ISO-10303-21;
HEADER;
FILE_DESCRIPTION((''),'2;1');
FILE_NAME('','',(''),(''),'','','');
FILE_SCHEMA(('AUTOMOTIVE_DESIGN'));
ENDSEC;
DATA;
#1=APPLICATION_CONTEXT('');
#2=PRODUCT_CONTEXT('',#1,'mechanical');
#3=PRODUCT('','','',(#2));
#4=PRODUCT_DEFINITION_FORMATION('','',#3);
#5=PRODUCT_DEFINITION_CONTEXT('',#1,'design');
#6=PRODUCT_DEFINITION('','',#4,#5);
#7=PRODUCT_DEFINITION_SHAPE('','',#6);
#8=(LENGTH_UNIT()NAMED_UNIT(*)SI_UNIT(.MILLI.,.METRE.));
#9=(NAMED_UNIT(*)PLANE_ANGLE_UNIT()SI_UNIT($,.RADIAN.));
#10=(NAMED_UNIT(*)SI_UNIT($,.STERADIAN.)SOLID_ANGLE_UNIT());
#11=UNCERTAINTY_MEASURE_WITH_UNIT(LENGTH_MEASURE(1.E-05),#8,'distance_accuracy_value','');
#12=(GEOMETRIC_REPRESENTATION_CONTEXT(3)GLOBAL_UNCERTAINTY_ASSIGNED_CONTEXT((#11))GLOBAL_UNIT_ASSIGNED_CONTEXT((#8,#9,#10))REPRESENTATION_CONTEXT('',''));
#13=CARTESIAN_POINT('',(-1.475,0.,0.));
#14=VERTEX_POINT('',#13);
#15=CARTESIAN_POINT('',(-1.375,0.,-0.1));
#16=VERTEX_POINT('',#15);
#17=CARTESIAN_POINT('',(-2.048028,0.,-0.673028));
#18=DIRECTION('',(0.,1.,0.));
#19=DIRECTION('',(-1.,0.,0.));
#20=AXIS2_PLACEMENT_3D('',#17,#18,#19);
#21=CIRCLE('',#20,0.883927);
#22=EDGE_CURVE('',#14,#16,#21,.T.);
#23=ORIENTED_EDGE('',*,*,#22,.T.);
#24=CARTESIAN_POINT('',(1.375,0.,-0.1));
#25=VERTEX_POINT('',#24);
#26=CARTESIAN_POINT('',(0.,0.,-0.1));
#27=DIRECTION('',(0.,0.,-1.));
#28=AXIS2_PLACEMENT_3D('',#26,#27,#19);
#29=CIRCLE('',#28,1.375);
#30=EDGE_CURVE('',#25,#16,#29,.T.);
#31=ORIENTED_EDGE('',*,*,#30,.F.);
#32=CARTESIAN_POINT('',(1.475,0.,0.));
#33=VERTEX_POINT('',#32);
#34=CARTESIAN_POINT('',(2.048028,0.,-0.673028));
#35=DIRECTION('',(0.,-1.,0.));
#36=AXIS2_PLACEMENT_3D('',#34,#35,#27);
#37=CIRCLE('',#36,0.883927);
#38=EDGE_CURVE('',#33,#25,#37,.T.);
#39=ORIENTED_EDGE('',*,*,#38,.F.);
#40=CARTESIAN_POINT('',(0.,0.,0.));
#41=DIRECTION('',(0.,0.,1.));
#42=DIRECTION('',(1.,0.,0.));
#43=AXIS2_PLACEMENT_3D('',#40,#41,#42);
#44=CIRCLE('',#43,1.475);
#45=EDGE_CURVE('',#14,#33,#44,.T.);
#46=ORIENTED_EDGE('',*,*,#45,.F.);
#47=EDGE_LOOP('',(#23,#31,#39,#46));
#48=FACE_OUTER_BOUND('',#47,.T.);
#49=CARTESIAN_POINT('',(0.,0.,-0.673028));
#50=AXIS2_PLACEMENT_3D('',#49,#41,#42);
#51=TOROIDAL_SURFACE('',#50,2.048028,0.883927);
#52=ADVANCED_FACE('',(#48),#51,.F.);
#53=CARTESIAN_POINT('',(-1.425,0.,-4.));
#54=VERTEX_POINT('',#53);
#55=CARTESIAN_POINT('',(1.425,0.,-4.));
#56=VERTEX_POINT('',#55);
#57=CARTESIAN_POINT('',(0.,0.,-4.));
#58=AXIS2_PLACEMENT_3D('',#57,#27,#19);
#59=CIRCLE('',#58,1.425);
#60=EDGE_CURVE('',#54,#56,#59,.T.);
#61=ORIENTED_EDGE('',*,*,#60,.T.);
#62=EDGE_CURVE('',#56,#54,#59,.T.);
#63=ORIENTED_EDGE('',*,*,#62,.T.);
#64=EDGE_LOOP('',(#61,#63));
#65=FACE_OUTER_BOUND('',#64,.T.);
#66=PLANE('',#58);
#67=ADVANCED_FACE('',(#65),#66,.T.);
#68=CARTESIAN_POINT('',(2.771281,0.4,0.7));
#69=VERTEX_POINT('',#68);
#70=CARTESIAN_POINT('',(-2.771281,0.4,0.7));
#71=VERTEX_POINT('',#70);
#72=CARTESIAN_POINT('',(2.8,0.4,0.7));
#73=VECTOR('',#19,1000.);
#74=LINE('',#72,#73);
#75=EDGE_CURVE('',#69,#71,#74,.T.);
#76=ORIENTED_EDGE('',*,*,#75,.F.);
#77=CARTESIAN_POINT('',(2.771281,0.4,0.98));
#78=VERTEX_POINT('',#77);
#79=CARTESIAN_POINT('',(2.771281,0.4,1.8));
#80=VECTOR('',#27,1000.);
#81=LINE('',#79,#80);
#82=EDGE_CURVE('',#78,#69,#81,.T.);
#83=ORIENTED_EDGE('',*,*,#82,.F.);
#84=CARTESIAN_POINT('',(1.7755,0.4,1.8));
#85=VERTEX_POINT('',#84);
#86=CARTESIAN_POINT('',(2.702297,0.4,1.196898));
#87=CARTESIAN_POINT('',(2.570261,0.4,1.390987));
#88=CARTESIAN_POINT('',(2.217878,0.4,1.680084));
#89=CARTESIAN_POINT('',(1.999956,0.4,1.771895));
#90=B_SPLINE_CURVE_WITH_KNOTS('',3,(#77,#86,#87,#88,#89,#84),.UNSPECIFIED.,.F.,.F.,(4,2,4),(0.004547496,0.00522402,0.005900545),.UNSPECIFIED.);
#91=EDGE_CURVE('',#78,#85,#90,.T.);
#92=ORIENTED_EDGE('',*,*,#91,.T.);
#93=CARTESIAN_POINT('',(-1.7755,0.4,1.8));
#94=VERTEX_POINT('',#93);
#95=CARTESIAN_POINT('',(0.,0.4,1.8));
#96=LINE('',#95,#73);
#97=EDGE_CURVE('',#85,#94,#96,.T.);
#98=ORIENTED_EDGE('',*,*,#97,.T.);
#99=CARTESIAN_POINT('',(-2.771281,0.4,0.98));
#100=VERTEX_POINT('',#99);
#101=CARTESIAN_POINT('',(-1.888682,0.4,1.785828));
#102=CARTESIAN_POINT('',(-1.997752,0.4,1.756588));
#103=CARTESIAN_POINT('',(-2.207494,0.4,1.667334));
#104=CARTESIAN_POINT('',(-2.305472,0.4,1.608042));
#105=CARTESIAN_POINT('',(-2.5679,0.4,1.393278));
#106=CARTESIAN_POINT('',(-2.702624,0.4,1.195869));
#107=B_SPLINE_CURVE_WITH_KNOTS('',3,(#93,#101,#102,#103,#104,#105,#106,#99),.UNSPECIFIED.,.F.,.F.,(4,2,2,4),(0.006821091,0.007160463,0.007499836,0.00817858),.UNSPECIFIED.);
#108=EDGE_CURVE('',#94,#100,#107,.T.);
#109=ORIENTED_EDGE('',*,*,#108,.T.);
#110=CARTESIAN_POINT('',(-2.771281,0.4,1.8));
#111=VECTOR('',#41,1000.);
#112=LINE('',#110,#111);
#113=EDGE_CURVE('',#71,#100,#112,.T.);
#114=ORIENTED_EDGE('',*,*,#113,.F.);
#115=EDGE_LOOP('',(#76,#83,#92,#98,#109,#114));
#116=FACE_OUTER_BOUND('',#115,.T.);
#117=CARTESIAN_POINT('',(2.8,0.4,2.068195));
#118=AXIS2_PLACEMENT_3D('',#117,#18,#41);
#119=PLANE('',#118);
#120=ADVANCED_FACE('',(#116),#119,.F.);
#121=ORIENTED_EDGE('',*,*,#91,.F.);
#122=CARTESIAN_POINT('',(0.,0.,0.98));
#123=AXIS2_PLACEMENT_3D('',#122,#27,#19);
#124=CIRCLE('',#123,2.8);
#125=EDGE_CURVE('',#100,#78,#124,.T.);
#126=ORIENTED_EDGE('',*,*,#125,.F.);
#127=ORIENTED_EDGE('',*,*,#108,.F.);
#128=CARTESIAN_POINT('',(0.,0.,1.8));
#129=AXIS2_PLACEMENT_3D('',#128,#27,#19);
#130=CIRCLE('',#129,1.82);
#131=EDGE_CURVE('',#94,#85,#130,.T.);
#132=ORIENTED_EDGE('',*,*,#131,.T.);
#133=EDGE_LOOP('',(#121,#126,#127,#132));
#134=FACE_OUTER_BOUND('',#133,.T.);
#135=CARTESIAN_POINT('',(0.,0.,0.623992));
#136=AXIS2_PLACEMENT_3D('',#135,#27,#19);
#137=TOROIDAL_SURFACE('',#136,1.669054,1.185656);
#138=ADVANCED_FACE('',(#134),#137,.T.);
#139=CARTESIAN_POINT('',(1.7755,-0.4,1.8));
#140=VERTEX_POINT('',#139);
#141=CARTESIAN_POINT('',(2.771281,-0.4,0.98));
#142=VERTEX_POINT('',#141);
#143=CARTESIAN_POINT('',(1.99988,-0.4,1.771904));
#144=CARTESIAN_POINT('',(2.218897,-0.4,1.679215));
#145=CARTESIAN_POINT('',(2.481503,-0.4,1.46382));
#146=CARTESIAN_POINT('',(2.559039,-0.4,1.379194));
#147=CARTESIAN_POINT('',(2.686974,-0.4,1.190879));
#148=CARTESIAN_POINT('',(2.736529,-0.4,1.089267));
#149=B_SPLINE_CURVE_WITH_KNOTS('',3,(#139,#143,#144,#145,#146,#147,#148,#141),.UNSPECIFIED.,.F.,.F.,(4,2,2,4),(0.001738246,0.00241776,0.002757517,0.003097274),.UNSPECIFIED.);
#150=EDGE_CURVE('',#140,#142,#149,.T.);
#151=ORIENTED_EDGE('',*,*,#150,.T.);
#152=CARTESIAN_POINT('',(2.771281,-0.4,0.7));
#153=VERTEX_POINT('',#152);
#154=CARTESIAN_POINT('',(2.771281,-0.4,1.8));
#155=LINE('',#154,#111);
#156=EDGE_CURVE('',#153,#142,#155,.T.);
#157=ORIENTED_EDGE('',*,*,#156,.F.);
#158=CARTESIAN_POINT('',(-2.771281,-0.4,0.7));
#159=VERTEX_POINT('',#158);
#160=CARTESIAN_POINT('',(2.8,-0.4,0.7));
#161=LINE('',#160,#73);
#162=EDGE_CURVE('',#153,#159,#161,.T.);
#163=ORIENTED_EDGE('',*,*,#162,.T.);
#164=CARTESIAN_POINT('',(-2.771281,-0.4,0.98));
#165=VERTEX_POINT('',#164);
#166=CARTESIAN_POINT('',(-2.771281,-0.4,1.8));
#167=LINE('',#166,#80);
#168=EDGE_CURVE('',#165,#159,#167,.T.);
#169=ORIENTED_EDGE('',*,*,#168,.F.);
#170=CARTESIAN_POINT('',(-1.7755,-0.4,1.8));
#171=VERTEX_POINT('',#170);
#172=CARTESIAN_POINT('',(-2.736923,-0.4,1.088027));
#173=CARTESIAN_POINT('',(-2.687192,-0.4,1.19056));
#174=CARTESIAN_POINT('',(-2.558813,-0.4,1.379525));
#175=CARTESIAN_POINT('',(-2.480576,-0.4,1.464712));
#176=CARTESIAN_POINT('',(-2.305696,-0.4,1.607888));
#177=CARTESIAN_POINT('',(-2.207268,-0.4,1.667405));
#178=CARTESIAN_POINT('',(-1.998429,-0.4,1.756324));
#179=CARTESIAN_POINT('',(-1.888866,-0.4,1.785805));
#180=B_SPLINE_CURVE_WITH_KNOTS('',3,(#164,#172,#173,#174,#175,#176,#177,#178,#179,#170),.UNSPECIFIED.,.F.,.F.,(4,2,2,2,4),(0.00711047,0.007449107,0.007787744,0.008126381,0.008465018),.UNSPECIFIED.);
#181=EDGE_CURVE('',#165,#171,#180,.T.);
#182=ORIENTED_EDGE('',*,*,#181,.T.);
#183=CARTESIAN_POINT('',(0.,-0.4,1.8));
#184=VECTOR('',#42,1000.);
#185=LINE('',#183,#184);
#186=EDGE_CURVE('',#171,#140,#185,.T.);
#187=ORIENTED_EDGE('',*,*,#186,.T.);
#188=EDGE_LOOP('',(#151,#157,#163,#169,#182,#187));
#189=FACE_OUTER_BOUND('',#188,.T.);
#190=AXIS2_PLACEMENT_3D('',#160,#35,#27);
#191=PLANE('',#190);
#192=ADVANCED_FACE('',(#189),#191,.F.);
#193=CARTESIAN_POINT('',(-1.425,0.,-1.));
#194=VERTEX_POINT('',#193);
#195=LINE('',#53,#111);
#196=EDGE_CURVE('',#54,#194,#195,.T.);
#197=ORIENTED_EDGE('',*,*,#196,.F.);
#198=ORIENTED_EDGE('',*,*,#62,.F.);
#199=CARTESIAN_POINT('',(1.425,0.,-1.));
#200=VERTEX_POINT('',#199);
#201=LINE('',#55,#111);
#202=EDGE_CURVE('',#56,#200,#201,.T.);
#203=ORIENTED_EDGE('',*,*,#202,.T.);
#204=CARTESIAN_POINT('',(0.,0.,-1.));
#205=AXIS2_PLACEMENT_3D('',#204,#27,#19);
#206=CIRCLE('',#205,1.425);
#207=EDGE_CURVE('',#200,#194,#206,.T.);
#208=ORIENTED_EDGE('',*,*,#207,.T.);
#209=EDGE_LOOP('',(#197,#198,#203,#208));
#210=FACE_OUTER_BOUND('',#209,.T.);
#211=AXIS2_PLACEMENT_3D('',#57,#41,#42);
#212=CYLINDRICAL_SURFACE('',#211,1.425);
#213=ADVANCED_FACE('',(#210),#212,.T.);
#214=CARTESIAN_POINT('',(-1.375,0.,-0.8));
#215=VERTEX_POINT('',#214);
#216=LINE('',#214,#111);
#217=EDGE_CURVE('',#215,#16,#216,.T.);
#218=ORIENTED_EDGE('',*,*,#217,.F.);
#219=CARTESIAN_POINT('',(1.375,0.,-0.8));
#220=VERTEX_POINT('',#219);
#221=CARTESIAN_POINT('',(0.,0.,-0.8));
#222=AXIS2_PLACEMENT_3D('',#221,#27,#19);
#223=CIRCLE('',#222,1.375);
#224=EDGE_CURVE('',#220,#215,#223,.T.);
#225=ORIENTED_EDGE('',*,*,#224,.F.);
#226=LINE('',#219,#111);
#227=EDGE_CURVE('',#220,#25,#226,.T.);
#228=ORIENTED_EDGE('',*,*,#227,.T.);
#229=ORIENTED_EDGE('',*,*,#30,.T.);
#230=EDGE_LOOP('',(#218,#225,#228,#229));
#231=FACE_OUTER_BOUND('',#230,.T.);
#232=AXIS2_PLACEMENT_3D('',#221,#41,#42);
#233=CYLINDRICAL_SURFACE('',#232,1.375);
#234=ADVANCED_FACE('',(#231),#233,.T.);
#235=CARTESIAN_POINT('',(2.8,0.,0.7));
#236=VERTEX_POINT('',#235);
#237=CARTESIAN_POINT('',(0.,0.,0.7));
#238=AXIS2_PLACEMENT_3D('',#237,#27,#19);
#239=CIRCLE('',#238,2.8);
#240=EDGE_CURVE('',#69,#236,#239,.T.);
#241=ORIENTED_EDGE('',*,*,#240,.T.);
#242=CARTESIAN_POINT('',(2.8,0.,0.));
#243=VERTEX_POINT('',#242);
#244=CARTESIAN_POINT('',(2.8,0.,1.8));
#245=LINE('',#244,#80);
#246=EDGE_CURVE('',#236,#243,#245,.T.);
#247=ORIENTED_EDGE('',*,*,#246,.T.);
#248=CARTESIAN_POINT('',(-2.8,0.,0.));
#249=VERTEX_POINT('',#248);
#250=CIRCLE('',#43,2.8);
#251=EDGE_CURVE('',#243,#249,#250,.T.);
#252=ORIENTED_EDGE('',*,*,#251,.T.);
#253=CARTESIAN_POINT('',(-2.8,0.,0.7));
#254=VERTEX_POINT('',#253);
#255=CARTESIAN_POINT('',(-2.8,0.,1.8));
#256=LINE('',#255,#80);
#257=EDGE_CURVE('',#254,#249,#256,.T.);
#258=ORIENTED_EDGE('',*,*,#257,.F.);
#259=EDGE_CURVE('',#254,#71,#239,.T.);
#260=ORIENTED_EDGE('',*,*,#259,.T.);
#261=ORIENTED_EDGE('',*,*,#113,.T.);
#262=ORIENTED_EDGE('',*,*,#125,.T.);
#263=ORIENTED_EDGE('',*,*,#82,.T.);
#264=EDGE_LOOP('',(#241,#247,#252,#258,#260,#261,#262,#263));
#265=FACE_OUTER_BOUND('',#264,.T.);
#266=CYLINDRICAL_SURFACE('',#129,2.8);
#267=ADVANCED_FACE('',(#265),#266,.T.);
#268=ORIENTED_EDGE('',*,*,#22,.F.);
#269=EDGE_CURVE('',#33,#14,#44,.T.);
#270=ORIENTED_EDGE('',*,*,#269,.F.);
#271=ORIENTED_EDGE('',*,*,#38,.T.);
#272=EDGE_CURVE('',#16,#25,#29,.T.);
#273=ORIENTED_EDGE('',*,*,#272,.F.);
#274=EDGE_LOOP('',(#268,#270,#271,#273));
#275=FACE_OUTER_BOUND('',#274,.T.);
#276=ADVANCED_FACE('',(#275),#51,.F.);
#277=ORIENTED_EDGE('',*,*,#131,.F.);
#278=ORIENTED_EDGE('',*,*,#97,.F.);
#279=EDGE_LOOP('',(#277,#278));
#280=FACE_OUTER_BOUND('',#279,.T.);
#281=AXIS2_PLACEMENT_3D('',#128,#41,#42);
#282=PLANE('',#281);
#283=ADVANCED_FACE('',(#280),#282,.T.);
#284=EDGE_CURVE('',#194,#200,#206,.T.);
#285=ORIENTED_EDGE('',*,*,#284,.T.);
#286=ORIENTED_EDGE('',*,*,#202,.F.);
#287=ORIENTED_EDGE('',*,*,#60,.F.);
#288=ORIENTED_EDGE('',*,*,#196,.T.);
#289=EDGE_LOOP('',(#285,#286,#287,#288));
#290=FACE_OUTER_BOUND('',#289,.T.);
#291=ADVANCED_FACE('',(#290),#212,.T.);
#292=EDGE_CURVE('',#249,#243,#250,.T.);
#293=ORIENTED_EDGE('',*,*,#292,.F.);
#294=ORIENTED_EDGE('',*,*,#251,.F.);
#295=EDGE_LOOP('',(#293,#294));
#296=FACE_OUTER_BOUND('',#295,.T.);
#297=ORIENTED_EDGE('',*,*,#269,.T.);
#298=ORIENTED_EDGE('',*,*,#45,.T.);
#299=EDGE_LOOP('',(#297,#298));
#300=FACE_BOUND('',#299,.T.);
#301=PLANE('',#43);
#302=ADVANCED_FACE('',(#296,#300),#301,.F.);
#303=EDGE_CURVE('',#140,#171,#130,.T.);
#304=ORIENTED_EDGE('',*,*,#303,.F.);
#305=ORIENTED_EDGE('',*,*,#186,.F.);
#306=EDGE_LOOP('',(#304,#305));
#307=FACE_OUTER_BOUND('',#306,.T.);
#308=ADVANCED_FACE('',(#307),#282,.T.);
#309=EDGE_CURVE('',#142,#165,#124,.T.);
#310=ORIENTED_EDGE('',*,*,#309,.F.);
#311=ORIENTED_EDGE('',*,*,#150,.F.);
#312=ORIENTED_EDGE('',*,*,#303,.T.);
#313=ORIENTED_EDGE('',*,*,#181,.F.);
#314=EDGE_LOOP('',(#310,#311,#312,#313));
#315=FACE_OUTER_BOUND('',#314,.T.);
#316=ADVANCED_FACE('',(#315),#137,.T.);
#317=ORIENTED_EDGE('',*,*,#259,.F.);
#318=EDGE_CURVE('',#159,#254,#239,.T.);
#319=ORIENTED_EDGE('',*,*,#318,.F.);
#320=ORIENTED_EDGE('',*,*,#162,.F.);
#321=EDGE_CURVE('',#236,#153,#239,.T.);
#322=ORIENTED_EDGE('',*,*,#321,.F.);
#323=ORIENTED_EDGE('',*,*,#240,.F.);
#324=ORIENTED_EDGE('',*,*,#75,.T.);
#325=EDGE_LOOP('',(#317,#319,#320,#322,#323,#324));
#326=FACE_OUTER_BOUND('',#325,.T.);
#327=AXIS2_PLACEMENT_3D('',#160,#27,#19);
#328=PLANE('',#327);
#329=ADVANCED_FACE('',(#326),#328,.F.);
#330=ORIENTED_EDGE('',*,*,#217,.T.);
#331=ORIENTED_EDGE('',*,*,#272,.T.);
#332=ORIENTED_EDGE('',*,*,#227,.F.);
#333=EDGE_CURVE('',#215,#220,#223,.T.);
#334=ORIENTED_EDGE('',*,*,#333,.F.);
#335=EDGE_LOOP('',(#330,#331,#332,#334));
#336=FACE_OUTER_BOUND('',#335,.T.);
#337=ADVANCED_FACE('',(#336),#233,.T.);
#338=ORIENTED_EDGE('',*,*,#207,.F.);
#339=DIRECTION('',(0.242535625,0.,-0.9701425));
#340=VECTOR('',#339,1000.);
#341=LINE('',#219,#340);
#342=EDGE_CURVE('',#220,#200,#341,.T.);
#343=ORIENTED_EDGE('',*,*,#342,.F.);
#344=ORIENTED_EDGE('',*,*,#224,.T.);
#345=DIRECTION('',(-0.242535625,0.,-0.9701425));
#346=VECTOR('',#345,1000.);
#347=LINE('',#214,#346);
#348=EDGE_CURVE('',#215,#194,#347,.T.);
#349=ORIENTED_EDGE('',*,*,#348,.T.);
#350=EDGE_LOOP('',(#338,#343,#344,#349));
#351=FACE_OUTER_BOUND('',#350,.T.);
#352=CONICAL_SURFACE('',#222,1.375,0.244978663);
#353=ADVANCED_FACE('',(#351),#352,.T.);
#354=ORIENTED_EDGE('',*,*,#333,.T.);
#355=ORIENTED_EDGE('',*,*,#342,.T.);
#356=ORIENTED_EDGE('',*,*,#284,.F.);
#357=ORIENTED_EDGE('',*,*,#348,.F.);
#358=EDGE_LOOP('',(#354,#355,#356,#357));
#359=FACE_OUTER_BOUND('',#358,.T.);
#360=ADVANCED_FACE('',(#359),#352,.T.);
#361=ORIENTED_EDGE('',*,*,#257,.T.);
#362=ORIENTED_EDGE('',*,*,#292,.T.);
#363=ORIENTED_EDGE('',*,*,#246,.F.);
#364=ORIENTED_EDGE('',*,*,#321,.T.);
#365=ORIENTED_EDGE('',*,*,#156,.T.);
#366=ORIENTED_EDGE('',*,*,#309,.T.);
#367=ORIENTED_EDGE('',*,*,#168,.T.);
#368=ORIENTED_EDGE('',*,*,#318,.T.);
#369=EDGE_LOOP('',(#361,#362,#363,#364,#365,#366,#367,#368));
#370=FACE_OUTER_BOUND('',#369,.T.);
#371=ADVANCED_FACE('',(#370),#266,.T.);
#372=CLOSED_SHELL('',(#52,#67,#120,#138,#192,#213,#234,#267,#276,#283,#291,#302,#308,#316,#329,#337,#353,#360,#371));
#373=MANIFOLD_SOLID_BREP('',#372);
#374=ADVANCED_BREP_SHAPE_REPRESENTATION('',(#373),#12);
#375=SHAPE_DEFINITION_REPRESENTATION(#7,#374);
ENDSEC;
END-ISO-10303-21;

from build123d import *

# Parameters (mm, degrees)
SKETCH_1_R           = 2.8
BOSS_EXTRUDE_1_DEPTH = 1.8
SKETCH_4_R           = 1.375
BOSS_EXTRUDE_2_DEPTH = 0.7
SKETCH_6_R           = 1.425
BOSS_EXTRUDE_3_DEPTH = 3
SKETCH_8_W           = 1.368195424
SKETCH_8_H           = 0.8
CUT_EXTRUDE_1_DEPTH  = 8.429670248


with BuildPart() as part:
    # Sketch 1 → Boss-Extrude 1 (new body)
    with BuildSketch(Plane.XY):
        Circle(SKETCH_1_R)
    extrude(amount=BOSS_EXTRUDE_1_DEPTH)

    # Sketch 3 → Revolve 1 (revolve)
    with BuildSketch(Plane(origin=(0, 0, 0), x_dir=(1, 0, 0), z_dir=(0, 1, 0))):
        with BuildLine():
            Line((0, 0), (1.475, 0))
            ThreePointArc((1.475, 0), (1.42299689, 0.04799689), (1.375, 0.1))
            Line((1.375, 0.1), (0, 0.1))
            Line((0, 0.1), (0, 0))
        make_face()
    revolve(axis=Axis((0, 0, 0), (0, 0, -1)))

    # Sketch 4 → Boss-Extrude 2 (add)
    with BuildSketch(Plane(origin=(0, 0, -0.1), x_dir=(-1, 0, 0), z_dir=(0, 0, -1))):
        Circle(SKETCH_4_R)
    extrude(amount=BOSS_EXTRUDE_2_DEPTH)

    # Sketch 5 → Revolve 2 (revolve)
    with BuildSketch(Plane(origin=(0, 0, 0), x_dir=(1, 0, 0), z_dir=(0, 1, 0)), mode=Mode.PRIVATE) as revolve_2_sk:
        Polygon((0, 0.8), (1.375, 0.8), (1.425, 1), (0, 1), align=None)
    revolve(revolve_2_sk.sketch.rotate(Axis((0, 0, 0), (0, 0, -1)), 180), axis=Axis((0, 0, 0), (0, 0, -1)))

    # Sketch 6 → Boss-Extrude 3 (add)
    with BuildSketch(Plane(origin=(0, 0, -1), x_dir=(-1, 0, 0), z_dir=(0, 0, -1))):
        Circle(SKETCH_6_R)
    extrude(amount=BOSS_EXTRUDE_3_DEPTH)

    # Sketch 7 → Cut-Revolve 3 (revolve, cut)
    with BuildSketch(Plane(origin=(0, 0, 0), x_dir=(1, 0, 0), z_dir=(0, 1, 0)), mode=Mode.PRIVATE) as cut_revolve_3_sk:
        with BuildLine():
            Line((1.82, -1.8), (2.8, -1.8))
            Line((2.8, -1.8), (2.8, -0.98))
            ThreePointArc((2.8, -0.98), (2.429916567, -1.533314921), (1.82, -1.8))
        make_face()
    revolve(cut_revolve_3_sk.sketch.rotate(Axis((0, 0, -0.11680497), (0, 0, 1)), 180), axis=Axis((0, 0, -0.11680497), (0, 0, 1)), mode=Mode.SUBTRACT)

    # Sketch 8 → Cut-Extrude 1 (cut, through all)
    with BuildSketch(Plane.ZY.offset(2.8)):
        with Locations((1.384097712, 0)):
            Rectangle(SKETCH_8_W, SKETCH_8_H)
    extrude(amount=-CUT_EXTRUDE_1_DEPTH, mode=Mode.SUBTRACT)


solid = part.part
